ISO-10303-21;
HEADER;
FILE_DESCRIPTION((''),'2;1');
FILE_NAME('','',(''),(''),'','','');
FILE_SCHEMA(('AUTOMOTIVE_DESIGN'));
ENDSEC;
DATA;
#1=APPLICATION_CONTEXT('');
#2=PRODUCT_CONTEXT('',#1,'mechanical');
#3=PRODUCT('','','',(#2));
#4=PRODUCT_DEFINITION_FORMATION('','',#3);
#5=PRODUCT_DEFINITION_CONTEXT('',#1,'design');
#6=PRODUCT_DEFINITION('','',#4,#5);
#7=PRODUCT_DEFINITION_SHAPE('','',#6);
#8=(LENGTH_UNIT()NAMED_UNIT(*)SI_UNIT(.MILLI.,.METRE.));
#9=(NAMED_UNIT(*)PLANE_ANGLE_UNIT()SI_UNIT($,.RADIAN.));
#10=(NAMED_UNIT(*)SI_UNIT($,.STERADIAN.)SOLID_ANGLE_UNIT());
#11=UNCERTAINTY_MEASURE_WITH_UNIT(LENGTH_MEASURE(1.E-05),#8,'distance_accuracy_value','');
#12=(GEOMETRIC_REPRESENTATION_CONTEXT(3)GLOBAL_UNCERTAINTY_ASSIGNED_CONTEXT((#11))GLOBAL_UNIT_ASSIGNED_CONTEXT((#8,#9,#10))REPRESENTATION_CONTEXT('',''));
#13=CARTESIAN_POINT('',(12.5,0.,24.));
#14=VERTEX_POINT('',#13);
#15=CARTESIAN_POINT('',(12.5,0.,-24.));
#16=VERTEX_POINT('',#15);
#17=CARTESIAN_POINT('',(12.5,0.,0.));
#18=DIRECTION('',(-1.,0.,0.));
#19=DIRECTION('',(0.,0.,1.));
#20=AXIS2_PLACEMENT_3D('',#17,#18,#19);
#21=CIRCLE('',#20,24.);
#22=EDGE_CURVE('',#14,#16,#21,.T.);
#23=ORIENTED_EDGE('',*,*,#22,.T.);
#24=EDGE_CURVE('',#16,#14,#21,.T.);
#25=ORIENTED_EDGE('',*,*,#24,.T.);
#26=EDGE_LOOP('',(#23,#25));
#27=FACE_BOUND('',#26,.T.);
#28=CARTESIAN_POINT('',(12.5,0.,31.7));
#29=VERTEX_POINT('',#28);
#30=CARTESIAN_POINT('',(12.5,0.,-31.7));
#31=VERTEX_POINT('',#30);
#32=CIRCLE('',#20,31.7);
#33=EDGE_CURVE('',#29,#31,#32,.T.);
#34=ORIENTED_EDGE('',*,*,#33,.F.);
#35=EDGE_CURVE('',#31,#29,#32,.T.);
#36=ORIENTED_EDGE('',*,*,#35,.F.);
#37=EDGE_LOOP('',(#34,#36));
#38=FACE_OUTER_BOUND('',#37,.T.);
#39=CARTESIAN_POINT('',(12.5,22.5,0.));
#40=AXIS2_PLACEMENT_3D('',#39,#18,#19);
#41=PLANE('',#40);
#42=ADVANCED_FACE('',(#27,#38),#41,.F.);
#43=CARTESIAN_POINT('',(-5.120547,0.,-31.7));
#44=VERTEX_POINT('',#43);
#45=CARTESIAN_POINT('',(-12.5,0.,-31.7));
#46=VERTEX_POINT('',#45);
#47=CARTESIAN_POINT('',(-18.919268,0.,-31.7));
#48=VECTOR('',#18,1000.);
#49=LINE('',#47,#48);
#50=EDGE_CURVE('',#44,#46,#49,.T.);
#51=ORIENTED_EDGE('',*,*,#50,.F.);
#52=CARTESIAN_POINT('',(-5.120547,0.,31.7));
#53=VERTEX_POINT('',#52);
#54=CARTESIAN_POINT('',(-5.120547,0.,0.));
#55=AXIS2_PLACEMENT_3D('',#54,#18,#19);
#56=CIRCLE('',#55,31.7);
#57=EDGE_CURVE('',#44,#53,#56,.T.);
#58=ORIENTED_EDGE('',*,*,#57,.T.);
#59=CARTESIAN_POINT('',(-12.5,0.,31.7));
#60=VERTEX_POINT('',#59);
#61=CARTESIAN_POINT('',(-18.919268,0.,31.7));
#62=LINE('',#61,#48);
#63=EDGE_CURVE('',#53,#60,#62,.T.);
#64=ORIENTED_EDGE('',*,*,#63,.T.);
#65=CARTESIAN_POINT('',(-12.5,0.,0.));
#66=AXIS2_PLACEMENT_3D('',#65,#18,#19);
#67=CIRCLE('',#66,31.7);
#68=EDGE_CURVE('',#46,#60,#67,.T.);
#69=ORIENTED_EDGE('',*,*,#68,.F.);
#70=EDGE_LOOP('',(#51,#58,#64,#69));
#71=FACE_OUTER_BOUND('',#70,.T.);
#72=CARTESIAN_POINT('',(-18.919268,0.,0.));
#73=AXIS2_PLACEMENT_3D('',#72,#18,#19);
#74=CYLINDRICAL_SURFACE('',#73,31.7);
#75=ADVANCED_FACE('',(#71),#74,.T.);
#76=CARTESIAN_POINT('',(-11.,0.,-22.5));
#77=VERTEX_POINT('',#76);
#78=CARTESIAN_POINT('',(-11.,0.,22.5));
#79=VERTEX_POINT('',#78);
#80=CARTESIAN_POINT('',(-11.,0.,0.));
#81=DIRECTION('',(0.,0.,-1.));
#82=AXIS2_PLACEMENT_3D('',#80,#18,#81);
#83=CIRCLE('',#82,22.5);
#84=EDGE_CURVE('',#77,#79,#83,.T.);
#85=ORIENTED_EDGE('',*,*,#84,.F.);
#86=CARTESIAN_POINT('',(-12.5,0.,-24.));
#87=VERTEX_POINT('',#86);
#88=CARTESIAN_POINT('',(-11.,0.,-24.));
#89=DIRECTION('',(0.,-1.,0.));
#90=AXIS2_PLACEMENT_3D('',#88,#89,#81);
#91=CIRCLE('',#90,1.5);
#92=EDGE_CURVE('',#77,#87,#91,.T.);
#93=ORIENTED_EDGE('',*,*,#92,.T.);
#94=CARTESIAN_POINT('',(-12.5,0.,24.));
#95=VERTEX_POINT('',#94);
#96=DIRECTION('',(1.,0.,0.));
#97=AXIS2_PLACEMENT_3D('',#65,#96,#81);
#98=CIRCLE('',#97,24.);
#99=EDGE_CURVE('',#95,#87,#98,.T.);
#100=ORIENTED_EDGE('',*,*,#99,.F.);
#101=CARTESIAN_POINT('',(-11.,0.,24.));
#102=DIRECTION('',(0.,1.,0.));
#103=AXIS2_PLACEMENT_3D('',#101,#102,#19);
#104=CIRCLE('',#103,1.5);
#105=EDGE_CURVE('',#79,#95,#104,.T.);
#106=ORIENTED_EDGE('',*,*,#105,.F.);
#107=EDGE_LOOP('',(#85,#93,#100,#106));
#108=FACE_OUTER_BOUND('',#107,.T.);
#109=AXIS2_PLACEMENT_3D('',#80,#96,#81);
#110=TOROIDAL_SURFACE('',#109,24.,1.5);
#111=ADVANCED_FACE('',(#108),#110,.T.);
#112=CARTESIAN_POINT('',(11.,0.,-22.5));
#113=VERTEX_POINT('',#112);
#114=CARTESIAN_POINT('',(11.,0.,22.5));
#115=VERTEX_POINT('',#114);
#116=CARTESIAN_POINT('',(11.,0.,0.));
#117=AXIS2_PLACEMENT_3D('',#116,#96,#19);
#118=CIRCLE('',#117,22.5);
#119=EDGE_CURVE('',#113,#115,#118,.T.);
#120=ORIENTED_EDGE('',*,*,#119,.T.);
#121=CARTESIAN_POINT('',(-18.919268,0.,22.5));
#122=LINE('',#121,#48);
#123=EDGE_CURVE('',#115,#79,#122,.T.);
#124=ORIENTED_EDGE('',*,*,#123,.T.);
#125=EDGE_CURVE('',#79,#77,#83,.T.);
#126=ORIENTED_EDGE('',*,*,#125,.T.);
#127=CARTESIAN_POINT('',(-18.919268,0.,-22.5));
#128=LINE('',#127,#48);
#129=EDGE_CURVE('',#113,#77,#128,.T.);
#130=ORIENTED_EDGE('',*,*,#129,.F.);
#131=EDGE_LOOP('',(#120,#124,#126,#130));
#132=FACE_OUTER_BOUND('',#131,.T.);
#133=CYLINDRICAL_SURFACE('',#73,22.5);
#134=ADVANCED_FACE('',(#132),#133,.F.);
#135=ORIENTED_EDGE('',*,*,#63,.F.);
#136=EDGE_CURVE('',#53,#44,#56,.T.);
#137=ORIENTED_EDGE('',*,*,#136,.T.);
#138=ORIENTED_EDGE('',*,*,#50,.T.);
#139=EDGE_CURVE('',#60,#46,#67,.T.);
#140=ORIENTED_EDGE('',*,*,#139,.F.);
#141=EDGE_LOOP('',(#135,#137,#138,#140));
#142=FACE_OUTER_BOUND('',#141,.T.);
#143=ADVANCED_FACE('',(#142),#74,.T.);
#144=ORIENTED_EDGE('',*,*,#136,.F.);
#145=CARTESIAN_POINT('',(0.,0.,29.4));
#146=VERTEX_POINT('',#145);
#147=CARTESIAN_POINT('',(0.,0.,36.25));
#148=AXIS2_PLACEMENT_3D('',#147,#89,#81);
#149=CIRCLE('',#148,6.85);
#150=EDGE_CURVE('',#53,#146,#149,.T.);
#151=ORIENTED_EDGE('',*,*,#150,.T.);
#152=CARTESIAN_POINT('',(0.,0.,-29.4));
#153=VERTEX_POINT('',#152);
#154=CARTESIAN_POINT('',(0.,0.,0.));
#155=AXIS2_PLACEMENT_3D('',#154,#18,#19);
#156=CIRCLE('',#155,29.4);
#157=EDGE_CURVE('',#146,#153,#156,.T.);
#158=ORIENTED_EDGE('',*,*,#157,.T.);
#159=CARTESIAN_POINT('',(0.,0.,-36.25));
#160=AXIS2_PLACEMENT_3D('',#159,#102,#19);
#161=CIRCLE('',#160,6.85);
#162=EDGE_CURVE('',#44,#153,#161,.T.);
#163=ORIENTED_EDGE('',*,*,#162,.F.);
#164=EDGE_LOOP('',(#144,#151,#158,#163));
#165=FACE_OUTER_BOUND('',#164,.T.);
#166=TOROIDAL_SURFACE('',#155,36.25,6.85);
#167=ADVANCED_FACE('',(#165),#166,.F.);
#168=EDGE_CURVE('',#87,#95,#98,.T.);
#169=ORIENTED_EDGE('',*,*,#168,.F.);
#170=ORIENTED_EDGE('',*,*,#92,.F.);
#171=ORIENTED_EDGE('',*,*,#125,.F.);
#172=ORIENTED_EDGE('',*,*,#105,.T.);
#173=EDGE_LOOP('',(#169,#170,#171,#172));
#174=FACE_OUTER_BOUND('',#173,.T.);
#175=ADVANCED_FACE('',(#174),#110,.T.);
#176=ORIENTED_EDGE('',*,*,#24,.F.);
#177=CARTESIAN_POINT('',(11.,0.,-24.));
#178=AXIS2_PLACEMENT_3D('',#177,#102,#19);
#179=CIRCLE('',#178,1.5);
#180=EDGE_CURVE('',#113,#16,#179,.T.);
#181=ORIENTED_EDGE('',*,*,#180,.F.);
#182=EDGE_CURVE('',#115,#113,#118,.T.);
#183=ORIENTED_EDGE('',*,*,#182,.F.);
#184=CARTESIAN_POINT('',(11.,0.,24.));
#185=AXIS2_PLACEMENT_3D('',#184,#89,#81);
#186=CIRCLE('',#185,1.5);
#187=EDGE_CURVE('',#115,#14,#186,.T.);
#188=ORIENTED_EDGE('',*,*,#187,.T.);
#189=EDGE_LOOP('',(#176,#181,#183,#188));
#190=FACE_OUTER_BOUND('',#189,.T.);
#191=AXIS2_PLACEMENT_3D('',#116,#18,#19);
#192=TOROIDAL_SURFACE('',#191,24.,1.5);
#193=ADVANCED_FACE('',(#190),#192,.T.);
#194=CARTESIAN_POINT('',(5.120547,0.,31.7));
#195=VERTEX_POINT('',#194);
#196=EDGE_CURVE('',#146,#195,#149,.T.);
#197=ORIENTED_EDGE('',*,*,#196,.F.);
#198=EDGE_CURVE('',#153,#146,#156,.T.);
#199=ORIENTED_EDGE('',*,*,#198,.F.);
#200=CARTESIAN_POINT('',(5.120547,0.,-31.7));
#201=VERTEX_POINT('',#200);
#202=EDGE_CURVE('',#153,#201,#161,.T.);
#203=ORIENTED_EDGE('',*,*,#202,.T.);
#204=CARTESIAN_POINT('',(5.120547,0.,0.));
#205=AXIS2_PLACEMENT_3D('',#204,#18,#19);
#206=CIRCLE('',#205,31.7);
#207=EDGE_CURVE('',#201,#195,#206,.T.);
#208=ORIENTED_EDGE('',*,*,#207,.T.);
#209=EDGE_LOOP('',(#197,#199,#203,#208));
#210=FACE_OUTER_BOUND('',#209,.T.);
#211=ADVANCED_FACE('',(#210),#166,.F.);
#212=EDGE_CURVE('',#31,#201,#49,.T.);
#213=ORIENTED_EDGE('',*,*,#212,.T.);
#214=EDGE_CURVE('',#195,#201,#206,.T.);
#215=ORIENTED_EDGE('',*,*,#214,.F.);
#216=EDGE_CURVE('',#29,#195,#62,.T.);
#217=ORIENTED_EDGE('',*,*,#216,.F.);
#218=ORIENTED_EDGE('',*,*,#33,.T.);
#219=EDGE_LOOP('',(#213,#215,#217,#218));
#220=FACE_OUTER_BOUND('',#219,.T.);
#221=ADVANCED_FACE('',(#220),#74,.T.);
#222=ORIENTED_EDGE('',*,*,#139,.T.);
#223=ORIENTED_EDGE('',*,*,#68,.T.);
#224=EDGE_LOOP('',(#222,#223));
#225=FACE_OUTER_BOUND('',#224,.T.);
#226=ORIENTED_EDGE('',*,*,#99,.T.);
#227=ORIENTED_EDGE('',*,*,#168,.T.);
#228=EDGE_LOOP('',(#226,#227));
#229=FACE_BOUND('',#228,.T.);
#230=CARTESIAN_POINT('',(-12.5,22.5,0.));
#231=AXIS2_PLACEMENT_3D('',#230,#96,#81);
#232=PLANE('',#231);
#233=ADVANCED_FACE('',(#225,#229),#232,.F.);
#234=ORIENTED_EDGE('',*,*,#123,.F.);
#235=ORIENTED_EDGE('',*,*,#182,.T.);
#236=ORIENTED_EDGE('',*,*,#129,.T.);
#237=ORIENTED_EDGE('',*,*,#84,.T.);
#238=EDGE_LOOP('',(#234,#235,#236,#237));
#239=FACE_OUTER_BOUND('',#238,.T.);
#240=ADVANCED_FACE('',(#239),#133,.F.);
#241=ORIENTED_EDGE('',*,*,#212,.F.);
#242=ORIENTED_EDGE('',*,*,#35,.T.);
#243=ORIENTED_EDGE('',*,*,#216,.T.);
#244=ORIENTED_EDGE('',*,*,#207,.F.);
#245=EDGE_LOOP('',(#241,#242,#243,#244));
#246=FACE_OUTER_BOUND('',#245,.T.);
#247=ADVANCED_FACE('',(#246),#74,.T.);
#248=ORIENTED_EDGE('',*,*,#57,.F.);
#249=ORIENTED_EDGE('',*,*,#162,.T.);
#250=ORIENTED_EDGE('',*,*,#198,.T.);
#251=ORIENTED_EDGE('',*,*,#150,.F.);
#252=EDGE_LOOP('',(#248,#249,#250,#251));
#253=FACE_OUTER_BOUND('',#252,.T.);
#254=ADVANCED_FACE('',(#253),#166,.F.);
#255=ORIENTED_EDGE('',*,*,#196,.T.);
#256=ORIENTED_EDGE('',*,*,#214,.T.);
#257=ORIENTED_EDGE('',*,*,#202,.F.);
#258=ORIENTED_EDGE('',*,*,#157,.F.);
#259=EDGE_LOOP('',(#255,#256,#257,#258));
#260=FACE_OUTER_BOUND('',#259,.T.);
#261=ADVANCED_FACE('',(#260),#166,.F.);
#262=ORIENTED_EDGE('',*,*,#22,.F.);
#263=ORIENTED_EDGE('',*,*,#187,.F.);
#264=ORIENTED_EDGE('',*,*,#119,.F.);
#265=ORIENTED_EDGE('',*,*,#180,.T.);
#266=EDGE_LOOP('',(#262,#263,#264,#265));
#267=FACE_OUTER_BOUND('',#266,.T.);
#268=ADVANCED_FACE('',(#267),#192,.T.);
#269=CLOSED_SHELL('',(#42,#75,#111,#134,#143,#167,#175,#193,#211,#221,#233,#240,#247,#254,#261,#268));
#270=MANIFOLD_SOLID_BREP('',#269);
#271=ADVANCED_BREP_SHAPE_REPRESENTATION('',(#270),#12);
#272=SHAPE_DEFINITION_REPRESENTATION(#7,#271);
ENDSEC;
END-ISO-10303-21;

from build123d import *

# Parameters (mm, degrees)
FILLET1_R = 1.5


with BuildPart() as part:
    # Sketch1 → Revolve1 (revolve)
    with BuildSketch(Plane.XY, mode=Mode.PRIVATE) as revolve1_sk:
        with BuildLine():
            Line((5.120546846, 31.7), (12.5, 31.7))
            Line((12.5, 31.7), (12.5, 22.5))
            Line((12.5, 22.5), (-12.5, 22.5))
            Line((-12.5, 22.5), (-12.5, 31.7))
            Line((-12.5, 31.7), (-5.120546846, 31.7))
            ThreePointArc((-5.120546846, 31.7), (0, 29.4), (5.120546846, 31.7))
        make_face()
    revolve(revolve1_sk.sketch.rotate(Axis((-18.919268053, 0, 0), (1, 0, 0)), 90), axis=Axis((-18.919268053, 0, 0), (1, 0, 0)))

    # Fillet1
    fillet1_edges = [part.edges().sort_by_distance(p)[0] for p in [
        (12.5, 0, -22.5),
        (-12.5, 0, -22.5),
    ]]
    fillet(fillet1_edges, radius=FILLET1_R)


solid = part.part
